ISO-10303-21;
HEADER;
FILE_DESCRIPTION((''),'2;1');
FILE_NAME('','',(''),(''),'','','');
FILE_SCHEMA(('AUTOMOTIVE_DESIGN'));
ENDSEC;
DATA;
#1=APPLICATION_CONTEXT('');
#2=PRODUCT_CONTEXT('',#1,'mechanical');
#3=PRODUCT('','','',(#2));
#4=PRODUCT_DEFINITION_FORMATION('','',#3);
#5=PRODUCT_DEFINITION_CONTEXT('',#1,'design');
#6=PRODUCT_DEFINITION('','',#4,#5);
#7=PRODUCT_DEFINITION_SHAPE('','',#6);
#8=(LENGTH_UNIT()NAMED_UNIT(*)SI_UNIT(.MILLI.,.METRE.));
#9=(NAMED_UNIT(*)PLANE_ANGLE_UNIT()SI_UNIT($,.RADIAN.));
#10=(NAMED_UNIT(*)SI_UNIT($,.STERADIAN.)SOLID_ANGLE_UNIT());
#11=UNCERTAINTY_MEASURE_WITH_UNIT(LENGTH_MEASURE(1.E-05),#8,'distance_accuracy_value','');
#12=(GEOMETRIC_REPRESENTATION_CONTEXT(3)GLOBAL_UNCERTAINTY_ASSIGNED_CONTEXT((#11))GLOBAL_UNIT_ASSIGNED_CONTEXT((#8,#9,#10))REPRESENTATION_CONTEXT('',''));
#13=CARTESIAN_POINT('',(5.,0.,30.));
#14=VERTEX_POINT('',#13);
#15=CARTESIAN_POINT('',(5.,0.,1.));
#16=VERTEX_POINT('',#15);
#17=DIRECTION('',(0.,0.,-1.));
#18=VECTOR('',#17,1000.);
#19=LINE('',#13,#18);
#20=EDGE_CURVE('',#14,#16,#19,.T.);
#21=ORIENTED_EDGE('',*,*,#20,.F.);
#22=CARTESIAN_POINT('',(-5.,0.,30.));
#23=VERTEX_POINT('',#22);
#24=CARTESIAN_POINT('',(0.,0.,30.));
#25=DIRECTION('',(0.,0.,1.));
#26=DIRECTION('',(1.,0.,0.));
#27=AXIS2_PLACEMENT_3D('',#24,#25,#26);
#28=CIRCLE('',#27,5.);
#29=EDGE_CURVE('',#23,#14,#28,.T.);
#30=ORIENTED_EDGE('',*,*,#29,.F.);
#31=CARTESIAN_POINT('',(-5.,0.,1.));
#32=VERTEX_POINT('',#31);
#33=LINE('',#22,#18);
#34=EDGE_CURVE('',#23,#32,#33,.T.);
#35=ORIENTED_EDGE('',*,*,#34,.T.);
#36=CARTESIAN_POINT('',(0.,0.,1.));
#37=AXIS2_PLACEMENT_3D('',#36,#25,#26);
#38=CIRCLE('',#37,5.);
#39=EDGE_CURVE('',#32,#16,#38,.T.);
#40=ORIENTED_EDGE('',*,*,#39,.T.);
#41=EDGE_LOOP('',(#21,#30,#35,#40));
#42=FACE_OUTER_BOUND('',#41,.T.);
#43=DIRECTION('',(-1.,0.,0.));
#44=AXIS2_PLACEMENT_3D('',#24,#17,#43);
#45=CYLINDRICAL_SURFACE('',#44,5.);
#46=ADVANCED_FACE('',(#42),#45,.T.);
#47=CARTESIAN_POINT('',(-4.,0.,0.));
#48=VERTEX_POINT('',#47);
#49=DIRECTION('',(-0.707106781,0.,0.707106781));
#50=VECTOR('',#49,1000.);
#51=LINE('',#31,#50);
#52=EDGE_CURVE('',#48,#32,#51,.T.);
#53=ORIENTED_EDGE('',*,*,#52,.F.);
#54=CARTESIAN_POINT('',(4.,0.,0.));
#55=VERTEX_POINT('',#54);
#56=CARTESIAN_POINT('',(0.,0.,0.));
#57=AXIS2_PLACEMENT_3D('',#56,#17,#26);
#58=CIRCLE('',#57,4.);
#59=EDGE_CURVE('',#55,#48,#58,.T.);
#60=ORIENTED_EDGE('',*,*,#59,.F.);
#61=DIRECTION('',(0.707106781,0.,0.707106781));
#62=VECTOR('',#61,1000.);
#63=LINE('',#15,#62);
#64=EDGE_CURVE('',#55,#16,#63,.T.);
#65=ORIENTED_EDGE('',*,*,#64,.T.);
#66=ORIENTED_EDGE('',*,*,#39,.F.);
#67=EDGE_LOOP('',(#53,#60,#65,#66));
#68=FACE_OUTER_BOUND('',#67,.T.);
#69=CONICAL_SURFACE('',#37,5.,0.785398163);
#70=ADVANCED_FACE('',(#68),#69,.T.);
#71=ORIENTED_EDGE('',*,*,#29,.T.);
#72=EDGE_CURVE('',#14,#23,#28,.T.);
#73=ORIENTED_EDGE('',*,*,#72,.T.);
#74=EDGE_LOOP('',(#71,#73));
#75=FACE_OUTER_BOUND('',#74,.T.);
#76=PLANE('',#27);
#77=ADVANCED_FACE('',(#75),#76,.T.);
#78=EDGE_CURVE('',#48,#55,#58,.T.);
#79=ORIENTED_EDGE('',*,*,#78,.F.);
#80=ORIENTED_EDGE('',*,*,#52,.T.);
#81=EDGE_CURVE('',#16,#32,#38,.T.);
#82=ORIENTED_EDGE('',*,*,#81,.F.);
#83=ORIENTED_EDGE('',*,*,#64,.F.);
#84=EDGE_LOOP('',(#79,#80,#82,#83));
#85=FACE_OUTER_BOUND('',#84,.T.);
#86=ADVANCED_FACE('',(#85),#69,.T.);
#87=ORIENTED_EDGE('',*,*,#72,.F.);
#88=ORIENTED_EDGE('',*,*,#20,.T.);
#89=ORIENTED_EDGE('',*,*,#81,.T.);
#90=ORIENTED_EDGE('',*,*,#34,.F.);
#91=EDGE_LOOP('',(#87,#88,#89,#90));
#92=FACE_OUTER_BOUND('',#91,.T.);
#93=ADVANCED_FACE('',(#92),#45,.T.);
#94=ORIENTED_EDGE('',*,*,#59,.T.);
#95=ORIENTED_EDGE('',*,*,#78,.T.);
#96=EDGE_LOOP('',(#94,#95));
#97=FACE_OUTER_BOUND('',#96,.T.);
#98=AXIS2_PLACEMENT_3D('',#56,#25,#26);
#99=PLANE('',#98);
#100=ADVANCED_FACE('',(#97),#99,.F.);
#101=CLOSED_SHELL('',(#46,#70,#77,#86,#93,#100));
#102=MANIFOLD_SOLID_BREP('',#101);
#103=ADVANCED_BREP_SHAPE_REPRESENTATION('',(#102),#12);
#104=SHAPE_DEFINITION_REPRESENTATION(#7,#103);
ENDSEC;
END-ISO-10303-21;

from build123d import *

# Parameters (mm, degrees)
SKETCH1_R           = 5
BOSS_EXTRUDE1_DEPTH = 30
CHAMFER1_SIZE       = 1


with BuildPart() as part:
    # Sketch1 → Boss-Extrude1 (new body)
    with BuildSketch(Plane.XY):
        Circle(SKETCH1_R)
    extrude(amount=BOSS_EXTRUDE1_DEPTH)

    # Chamfer1
    chamfer1_edges = [part.edges().sort_by_distance(p)[0] for p in [
        (-5, 0, 0),
    ]]
    chamfer(chamfer1_edges, length=CHAMFER1_SIZE)


solid = part.part
